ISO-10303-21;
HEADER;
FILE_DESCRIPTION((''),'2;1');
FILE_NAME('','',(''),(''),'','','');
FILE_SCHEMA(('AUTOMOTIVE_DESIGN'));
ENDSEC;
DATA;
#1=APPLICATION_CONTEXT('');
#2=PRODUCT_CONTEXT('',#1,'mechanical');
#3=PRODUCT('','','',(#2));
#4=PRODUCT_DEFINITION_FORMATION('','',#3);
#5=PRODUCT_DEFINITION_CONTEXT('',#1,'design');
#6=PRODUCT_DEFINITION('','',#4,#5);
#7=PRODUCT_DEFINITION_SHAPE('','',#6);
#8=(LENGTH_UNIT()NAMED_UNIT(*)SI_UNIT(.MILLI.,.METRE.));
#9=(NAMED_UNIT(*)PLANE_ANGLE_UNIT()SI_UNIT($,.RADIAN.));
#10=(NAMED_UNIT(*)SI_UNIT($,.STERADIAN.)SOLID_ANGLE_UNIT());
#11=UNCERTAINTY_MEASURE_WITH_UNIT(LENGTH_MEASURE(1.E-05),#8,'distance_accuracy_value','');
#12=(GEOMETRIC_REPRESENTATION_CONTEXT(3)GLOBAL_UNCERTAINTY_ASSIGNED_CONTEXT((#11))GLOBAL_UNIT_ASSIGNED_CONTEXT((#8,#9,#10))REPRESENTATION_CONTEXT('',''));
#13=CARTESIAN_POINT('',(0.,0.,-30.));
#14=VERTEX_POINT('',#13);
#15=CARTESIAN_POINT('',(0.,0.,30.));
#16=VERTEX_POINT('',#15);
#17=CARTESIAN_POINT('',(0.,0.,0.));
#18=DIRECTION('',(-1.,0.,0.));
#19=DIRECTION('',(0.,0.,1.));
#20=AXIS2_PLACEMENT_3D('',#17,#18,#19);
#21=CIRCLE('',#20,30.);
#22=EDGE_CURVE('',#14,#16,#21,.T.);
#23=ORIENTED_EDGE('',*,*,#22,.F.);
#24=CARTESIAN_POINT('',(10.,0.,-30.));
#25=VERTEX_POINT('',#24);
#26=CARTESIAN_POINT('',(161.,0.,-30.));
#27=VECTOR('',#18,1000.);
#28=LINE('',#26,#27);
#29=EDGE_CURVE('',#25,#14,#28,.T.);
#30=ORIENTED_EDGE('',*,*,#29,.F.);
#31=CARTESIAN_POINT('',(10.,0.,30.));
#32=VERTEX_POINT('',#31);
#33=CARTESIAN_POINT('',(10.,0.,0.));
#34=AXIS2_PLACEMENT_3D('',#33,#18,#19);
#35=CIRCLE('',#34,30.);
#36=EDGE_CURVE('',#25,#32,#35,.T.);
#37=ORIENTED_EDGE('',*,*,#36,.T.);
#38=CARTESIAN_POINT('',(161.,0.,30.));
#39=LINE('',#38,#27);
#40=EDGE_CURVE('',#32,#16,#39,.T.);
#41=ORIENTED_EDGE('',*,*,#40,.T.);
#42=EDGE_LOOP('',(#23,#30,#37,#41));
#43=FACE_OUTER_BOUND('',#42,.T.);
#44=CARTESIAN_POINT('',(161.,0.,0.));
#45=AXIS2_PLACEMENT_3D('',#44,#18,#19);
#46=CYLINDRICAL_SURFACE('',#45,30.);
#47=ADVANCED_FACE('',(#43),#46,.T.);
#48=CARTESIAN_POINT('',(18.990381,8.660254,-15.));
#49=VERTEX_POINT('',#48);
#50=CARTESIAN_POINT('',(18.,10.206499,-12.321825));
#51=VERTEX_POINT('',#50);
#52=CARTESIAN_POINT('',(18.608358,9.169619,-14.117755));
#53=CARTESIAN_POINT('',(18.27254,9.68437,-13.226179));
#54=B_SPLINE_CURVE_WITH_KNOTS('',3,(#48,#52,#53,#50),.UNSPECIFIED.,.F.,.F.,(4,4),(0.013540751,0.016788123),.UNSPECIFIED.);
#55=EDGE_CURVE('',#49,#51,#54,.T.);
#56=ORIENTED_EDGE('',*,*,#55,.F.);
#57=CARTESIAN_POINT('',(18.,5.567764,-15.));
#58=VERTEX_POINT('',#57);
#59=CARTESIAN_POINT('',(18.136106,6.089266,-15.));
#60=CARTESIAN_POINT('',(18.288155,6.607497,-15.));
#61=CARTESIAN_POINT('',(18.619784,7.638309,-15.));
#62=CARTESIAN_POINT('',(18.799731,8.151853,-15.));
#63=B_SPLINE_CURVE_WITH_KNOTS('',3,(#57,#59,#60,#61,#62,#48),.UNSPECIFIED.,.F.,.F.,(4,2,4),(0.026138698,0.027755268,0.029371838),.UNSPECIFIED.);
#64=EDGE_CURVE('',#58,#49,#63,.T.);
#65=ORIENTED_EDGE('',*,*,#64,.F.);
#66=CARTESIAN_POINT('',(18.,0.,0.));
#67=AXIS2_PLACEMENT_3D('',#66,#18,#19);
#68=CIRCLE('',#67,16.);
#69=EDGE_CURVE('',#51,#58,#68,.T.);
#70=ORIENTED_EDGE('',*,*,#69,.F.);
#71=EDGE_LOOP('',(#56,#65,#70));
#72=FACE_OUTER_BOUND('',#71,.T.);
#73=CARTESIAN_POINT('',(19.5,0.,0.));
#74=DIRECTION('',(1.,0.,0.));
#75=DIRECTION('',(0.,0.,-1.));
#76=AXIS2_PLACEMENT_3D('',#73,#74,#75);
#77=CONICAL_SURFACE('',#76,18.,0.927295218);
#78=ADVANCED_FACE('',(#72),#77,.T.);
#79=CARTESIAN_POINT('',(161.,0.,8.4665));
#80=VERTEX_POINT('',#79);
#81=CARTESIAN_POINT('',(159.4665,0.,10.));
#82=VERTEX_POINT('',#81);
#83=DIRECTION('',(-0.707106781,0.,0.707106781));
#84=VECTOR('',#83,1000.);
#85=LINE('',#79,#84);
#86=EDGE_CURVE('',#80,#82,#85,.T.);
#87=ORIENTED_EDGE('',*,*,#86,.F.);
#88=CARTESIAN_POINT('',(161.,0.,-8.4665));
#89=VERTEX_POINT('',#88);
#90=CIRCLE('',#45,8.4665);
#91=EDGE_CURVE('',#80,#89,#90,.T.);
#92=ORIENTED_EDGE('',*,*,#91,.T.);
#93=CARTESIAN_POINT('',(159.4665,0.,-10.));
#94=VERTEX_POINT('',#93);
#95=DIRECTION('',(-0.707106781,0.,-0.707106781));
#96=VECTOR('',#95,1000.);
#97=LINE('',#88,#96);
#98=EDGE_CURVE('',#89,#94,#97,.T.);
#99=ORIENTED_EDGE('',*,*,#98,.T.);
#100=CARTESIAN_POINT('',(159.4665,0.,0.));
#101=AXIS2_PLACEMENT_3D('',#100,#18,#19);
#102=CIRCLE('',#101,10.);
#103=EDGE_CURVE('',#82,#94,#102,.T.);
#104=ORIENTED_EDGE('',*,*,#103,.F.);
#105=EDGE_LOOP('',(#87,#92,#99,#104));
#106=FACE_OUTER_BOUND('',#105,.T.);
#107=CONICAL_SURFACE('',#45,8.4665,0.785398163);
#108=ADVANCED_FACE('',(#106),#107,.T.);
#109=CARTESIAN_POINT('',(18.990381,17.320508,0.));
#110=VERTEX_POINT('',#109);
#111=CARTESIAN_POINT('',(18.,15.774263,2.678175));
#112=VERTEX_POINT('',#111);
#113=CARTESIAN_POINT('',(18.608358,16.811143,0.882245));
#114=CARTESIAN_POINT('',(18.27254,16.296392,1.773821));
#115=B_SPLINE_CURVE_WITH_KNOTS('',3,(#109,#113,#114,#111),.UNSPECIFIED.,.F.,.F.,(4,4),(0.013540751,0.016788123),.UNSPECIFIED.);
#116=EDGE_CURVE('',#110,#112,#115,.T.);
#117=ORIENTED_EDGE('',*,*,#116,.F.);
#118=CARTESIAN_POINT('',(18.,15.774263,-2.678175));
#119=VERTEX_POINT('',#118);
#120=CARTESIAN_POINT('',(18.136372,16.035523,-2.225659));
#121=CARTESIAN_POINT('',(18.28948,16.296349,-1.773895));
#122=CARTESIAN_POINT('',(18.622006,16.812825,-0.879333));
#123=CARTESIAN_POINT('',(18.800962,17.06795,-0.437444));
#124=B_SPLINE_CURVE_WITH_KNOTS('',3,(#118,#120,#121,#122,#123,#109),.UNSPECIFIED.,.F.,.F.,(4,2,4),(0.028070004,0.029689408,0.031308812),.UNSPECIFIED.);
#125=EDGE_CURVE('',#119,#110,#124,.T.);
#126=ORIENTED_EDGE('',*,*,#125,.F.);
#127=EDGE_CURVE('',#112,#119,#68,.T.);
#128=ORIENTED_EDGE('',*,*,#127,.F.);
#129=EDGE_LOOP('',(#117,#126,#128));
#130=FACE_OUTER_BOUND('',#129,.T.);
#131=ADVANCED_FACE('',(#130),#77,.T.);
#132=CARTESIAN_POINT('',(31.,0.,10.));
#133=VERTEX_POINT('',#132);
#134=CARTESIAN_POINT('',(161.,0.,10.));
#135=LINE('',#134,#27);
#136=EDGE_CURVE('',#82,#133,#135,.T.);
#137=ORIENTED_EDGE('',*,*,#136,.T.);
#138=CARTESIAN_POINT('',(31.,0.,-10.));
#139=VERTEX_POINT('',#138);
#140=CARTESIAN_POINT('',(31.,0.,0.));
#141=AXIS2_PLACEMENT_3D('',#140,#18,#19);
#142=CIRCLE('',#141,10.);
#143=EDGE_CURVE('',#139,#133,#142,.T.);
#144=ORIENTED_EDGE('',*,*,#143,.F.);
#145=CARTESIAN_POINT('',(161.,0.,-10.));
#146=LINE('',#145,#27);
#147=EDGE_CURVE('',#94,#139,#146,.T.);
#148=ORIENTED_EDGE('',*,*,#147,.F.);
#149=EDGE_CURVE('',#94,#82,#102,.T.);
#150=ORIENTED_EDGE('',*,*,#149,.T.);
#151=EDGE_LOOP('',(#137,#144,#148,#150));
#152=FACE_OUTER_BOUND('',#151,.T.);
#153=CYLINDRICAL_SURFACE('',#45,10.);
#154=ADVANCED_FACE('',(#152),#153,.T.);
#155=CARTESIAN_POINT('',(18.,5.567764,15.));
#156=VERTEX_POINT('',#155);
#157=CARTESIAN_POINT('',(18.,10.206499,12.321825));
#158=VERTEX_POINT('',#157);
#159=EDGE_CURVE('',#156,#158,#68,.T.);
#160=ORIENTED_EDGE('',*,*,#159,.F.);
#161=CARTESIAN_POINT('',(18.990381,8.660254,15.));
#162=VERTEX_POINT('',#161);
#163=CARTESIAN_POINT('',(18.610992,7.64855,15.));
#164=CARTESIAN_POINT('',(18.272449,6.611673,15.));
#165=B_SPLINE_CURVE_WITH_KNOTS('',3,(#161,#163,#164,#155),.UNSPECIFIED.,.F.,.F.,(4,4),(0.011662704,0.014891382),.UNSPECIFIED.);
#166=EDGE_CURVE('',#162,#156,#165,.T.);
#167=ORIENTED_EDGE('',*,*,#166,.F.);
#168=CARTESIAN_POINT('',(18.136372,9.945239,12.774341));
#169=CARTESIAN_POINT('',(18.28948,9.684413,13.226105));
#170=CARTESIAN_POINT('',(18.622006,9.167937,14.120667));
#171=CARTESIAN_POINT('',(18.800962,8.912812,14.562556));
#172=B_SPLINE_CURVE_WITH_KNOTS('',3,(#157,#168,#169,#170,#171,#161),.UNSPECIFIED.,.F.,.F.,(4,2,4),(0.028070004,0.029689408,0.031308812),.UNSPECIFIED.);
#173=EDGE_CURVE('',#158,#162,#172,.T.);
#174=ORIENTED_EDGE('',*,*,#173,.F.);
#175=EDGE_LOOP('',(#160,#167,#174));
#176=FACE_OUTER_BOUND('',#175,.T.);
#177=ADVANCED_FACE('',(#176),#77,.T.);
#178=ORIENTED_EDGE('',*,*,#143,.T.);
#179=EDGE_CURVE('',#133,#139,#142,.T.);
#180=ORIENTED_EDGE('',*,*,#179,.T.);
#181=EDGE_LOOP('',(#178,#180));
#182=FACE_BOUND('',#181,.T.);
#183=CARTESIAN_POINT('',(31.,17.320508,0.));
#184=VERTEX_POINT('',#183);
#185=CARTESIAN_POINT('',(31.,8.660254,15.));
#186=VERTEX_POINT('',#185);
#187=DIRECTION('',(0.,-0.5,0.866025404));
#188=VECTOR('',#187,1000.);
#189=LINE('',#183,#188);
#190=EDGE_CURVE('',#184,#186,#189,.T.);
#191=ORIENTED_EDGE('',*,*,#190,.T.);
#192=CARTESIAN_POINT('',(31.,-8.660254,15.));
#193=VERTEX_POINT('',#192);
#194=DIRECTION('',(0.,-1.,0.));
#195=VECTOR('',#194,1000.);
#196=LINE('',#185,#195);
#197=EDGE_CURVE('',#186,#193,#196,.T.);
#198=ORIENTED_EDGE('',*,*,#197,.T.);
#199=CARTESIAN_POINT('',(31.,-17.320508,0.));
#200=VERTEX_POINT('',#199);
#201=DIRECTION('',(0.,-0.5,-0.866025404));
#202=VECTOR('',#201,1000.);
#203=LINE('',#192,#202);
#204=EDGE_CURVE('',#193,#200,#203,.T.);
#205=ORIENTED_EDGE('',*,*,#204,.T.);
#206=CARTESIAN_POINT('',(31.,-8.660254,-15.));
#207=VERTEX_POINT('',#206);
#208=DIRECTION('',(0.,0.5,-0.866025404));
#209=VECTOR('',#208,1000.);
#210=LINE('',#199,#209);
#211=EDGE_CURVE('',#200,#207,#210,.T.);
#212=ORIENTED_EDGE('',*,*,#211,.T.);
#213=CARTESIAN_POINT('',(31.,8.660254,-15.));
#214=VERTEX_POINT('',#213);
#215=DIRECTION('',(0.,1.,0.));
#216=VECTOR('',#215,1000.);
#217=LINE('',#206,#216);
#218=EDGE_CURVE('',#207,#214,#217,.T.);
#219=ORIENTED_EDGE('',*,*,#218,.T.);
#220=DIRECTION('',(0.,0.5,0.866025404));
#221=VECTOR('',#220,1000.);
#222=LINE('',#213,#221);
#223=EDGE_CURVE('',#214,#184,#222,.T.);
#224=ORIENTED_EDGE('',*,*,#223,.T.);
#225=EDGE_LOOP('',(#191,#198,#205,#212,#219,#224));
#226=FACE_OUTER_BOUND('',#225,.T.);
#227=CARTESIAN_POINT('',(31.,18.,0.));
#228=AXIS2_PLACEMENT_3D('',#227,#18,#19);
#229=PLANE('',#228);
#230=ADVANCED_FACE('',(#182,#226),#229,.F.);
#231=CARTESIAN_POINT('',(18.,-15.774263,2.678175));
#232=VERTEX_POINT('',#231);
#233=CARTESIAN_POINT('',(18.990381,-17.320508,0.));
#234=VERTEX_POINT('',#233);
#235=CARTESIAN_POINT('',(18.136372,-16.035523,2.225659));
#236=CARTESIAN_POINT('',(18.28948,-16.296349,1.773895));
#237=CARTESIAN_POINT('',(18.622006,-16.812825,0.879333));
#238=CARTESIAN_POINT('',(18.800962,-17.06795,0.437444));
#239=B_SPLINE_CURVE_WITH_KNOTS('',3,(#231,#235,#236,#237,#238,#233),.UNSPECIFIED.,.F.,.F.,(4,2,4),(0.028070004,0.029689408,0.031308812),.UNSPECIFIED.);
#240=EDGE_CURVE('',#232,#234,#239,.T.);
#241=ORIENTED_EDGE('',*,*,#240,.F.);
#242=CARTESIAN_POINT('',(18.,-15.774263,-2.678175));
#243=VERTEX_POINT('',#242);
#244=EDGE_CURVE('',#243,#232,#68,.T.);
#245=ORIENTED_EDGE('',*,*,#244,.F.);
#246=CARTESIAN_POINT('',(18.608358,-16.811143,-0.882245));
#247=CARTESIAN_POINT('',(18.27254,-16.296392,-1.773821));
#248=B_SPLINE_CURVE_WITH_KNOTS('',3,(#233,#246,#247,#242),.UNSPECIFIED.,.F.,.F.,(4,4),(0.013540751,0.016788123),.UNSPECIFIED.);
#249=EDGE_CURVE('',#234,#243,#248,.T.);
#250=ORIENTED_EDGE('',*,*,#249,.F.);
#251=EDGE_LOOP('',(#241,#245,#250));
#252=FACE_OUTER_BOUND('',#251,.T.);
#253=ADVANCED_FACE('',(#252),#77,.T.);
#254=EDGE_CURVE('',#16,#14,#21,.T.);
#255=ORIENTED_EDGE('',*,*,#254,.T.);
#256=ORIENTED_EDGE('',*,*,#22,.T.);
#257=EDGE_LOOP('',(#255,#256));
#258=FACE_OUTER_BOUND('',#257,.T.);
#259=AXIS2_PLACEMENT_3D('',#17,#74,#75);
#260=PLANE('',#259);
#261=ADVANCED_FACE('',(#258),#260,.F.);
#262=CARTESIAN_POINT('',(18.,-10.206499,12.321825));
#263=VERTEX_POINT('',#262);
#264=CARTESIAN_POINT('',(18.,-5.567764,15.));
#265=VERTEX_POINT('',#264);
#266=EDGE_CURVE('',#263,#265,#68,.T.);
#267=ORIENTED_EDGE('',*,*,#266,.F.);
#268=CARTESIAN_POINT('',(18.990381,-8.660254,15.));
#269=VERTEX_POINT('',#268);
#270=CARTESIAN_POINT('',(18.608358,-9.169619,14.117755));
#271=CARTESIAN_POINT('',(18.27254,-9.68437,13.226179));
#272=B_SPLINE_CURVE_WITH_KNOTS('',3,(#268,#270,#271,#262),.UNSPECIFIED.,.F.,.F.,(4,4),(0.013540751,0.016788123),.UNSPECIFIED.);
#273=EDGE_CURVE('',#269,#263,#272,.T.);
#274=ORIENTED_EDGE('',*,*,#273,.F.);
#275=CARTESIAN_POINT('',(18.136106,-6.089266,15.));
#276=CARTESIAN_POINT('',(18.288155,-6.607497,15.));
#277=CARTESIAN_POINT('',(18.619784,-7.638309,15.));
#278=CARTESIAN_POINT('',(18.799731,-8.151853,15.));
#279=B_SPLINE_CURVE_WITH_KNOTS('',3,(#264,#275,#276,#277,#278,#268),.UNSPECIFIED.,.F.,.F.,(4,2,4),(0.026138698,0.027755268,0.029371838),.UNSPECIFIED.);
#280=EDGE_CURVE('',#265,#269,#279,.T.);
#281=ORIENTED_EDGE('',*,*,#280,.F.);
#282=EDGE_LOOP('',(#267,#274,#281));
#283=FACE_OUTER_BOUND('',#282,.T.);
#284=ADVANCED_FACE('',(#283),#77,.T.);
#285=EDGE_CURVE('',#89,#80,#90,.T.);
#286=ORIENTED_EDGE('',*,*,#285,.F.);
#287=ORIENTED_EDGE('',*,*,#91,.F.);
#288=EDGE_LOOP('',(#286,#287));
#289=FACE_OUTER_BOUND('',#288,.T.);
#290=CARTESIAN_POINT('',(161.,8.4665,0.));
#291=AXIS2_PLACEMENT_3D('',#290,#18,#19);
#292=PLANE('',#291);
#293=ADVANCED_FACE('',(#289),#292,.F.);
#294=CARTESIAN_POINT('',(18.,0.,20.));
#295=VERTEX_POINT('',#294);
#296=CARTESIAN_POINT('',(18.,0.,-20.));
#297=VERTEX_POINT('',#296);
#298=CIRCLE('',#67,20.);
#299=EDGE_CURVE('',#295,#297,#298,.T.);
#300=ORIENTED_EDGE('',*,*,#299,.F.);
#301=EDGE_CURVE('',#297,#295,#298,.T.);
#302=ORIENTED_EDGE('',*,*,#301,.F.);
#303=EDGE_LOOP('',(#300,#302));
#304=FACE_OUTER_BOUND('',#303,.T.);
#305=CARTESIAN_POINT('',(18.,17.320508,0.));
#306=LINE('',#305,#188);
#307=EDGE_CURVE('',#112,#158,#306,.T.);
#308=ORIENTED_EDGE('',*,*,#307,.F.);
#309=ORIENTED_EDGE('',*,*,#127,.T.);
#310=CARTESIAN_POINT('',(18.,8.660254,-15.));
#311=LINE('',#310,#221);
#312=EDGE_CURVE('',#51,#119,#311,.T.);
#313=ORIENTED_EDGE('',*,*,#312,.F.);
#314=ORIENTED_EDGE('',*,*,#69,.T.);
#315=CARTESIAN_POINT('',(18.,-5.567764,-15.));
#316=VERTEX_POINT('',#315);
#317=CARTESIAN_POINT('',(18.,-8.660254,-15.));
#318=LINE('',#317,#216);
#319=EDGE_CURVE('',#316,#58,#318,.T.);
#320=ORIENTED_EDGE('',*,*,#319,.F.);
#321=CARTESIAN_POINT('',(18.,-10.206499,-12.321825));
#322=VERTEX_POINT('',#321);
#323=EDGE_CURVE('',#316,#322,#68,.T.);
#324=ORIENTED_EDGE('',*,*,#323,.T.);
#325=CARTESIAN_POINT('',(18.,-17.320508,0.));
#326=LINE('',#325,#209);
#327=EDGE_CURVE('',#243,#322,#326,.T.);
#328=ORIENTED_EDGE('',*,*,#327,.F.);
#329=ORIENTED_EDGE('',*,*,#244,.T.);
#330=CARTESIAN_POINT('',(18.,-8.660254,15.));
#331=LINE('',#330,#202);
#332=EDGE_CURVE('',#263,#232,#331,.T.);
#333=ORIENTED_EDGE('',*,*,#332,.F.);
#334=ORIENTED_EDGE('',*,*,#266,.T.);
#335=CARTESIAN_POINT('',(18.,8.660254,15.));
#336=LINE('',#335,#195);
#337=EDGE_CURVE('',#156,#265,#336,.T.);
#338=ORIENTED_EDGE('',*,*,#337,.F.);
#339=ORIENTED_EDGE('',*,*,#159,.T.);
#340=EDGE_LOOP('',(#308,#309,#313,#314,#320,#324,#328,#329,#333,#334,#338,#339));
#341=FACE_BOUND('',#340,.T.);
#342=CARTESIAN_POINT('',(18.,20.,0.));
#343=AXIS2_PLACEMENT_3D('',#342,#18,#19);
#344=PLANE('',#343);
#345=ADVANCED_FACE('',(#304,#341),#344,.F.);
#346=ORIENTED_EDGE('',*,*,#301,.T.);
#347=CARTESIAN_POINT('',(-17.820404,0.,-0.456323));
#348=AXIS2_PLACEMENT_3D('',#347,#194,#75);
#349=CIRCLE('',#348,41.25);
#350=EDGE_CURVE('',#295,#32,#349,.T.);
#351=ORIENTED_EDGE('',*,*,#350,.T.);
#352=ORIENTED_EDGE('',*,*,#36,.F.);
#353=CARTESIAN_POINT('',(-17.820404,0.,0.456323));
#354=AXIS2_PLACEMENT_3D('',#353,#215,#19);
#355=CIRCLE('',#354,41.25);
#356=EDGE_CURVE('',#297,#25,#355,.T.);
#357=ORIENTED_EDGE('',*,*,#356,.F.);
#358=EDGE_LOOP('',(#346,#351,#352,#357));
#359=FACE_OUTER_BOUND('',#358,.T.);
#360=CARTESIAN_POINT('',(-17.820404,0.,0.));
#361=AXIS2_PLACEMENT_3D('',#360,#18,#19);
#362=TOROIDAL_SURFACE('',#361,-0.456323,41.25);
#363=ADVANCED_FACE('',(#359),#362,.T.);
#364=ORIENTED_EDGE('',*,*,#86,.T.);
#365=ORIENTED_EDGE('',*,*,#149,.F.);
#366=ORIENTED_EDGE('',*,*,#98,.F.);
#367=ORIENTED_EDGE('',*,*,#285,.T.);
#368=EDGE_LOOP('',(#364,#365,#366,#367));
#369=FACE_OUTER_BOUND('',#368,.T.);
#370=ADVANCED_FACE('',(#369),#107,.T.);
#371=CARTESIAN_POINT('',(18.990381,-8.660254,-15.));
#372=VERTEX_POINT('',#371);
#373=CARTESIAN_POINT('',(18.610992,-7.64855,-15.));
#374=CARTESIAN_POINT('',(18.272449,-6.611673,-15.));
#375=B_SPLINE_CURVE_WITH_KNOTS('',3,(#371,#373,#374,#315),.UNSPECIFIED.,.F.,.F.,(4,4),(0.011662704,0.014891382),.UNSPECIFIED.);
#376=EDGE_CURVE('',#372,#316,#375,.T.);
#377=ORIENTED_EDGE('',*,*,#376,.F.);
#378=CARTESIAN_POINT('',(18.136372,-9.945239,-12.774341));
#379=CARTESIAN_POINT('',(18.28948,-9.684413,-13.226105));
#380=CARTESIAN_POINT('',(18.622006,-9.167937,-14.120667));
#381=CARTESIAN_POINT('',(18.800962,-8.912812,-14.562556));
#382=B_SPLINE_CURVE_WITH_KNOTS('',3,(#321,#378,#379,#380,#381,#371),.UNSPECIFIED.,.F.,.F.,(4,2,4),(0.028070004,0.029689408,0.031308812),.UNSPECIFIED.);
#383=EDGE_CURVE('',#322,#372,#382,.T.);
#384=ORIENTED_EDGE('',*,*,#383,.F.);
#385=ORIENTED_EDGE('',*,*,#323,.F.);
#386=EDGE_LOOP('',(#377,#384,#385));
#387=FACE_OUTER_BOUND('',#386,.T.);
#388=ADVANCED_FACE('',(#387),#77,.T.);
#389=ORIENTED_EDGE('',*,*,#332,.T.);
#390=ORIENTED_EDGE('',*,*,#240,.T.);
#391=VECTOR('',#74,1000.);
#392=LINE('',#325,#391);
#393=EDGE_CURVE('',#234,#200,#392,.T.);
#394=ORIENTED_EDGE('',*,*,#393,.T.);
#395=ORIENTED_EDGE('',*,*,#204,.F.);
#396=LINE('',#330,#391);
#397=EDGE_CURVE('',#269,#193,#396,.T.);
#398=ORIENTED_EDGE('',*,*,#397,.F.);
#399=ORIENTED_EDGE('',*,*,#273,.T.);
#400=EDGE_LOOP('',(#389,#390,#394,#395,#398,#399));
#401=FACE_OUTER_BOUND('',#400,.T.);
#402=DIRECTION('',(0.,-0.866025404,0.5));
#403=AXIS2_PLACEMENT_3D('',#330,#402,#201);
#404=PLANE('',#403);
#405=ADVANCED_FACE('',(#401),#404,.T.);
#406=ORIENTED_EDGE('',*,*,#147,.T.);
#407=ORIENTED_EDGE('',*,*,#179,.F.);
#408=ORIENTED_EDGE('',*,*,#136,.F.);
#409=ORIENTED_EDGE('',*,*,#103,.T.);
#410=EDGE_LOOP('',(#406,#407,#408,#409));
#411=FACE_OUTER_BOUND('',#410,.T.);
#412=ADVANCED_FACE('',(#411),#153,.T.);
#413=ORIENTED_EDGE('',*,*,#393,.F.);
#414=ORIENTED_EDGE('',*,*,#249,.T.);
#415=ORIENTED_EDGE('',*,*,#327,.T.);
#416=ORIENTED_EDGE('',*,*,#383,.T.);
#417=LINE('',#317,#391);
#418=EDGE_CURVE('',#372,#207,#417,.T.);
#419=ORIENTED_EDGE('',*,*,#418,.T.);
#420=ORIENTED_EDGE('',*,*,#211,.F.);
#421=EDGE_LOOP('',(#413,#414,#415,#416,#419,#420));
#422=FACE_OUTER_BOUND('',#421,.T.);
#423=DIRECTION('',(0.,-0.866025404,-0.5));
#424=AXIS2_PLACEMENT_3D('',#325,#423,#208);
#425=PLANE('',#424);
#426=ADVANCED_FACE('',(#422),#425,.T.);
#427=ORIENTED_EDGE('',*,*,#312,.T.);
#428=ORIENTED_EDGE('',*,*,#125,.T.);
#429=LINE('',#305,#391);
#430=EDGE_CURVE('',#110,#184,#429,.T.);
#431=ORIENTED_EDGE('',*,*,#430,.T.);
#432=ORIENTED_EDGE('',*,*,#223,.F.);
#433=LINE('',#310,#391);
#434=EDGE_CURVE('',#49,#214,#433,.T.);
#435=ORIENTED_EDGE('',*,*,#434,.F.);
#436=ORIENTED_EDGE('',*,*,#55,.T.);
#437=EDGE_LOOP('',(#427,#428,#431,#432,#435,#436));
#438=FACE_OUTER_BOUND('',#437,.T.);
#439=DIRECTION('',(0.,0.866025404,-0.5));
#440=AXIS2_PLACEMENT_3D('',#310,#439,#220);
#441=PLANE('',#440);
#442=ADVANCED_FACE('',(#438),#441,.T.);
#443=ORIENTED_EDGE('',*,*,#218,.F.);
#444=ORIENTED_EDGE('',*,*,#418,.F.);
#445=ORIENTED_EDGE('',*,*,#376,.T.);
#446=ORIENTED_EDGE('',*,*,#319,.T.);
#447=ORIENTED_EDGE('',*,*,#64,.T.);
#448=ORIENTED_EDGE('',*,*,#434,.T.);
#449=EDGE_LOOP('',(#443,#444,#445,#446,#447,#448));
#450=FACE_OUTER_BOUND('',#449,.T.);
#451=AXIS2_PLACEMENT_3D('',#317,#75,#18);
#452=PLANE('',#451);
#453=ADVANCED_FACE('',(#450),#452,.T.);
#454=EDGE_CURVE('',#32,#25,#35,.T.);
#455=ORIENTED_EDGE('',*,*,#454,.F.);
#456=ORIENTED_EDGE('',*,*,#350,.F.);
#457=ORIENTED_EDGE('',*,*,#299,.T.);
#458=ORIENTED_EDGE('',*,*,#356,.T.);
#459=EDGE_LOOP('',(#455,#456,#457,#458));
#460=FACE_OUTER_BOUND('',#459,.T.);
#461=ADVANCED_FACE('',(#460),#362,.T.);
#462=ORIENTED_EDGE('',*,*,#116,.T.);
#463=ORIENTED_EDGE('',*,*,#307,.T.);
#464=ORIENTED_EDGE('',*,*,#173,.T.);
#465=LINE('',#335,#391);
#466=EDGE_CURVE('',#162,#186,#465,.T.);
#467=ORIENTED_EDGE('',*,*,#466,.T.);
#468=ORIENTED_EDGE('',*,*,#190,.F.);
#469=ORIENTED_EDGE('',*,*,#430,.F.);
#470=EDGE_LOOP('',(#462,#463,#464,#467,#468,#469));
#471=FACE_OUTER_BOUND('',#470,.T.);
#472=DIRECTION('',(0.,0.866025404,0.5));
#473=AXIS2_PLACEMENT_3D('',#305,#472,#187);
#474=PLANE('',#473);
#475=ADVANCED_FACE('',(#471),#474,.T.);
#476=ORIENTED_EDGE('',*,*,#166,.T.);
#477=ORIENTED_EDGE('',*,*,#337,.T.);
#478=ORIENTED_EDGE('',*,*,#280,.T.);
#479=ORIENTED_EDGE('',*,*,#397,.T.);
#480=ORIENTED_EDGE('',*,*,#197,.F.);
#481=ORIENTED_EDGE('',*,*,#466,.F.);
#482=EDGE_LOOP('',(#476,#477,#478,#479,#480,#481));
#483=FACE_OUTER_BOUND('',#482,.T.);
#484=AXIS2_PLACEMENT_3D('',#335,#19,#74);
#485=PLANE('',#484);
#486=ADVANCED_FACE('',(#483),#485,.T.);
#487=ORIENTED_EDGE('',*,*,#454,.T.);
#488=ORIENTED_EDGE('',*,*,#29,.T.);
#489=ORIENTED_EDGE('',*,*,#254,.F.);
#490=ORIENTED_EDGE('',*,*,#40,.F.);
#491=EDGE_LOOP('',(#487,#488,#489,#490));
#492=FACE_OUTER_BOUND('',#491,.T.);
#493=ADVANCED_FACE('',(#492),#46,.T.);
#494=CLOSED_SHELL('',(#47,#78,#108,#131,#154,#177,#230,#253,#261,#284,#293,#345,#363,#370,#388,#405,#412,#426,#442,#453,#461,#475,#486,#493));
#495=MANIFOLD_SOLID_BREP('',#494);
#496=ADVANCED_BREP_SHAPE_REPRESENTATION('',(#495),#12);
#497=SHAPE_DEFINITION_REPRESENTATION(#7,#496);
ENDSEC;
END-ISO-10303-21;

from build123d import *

# Parameters (mm, degrees)
SKETCH2_R          = 19.5
CUT_EXTRUDE1_DEPTH = 13


with BuildPart() as part:
    # Sketch1 → Revolve1 (revolve)
    with BuildSketch(Plane.XY, mode=Mode.PRIVATE) as revolve1_sk:
        with BuildLine():
            Line((0, 0), (0, 30))
            Line((0, 30), (10, 30))
            ThreePointArc((10, 30), (14.390434405, 25.312347524), (18, 20))
            Line((18, 20), (18, 16))
            Line((18, 16), (19.5, 18))
            Line((19.5, 18), (31, 18))
            Line((31, 18), (31, 10))
            Line((31, 10), (159.4665, 10))
            Line((159.4665, 10), (161, 8.4665))
            Line((161, 8.4665), (161, 0))
            Line((161, 0), (0, 0))
        make_face()
    revolve(revolve1_sk.sketch.rotate(Axis((161, 0, 0), (-1, 0, 0)), 270), axis=Axis((161, 0, 0), (-1, 0, 0)))

    # Sketch2 → Cut-Extrude1 (cut)
    with BuildSketch(Plane(origin=(31, 0, 0), x_dir=(0, 0, -1), z_dir=(1, 0, 0))):
        Circle(SKETCH2_R)
        Polygon((-15, 8.660254038), (-15, -8.660254038), (0, -17.320508076), (15, -8.660254038), (15, 8.660254038), (0, 17.320508076), align=None, mode=Mode.SUBTRACT)
    extrude(amount=-CUT_EXTRUDE1_DEPTH, mode=Mode.SUBTRACT)


solid = part.part
